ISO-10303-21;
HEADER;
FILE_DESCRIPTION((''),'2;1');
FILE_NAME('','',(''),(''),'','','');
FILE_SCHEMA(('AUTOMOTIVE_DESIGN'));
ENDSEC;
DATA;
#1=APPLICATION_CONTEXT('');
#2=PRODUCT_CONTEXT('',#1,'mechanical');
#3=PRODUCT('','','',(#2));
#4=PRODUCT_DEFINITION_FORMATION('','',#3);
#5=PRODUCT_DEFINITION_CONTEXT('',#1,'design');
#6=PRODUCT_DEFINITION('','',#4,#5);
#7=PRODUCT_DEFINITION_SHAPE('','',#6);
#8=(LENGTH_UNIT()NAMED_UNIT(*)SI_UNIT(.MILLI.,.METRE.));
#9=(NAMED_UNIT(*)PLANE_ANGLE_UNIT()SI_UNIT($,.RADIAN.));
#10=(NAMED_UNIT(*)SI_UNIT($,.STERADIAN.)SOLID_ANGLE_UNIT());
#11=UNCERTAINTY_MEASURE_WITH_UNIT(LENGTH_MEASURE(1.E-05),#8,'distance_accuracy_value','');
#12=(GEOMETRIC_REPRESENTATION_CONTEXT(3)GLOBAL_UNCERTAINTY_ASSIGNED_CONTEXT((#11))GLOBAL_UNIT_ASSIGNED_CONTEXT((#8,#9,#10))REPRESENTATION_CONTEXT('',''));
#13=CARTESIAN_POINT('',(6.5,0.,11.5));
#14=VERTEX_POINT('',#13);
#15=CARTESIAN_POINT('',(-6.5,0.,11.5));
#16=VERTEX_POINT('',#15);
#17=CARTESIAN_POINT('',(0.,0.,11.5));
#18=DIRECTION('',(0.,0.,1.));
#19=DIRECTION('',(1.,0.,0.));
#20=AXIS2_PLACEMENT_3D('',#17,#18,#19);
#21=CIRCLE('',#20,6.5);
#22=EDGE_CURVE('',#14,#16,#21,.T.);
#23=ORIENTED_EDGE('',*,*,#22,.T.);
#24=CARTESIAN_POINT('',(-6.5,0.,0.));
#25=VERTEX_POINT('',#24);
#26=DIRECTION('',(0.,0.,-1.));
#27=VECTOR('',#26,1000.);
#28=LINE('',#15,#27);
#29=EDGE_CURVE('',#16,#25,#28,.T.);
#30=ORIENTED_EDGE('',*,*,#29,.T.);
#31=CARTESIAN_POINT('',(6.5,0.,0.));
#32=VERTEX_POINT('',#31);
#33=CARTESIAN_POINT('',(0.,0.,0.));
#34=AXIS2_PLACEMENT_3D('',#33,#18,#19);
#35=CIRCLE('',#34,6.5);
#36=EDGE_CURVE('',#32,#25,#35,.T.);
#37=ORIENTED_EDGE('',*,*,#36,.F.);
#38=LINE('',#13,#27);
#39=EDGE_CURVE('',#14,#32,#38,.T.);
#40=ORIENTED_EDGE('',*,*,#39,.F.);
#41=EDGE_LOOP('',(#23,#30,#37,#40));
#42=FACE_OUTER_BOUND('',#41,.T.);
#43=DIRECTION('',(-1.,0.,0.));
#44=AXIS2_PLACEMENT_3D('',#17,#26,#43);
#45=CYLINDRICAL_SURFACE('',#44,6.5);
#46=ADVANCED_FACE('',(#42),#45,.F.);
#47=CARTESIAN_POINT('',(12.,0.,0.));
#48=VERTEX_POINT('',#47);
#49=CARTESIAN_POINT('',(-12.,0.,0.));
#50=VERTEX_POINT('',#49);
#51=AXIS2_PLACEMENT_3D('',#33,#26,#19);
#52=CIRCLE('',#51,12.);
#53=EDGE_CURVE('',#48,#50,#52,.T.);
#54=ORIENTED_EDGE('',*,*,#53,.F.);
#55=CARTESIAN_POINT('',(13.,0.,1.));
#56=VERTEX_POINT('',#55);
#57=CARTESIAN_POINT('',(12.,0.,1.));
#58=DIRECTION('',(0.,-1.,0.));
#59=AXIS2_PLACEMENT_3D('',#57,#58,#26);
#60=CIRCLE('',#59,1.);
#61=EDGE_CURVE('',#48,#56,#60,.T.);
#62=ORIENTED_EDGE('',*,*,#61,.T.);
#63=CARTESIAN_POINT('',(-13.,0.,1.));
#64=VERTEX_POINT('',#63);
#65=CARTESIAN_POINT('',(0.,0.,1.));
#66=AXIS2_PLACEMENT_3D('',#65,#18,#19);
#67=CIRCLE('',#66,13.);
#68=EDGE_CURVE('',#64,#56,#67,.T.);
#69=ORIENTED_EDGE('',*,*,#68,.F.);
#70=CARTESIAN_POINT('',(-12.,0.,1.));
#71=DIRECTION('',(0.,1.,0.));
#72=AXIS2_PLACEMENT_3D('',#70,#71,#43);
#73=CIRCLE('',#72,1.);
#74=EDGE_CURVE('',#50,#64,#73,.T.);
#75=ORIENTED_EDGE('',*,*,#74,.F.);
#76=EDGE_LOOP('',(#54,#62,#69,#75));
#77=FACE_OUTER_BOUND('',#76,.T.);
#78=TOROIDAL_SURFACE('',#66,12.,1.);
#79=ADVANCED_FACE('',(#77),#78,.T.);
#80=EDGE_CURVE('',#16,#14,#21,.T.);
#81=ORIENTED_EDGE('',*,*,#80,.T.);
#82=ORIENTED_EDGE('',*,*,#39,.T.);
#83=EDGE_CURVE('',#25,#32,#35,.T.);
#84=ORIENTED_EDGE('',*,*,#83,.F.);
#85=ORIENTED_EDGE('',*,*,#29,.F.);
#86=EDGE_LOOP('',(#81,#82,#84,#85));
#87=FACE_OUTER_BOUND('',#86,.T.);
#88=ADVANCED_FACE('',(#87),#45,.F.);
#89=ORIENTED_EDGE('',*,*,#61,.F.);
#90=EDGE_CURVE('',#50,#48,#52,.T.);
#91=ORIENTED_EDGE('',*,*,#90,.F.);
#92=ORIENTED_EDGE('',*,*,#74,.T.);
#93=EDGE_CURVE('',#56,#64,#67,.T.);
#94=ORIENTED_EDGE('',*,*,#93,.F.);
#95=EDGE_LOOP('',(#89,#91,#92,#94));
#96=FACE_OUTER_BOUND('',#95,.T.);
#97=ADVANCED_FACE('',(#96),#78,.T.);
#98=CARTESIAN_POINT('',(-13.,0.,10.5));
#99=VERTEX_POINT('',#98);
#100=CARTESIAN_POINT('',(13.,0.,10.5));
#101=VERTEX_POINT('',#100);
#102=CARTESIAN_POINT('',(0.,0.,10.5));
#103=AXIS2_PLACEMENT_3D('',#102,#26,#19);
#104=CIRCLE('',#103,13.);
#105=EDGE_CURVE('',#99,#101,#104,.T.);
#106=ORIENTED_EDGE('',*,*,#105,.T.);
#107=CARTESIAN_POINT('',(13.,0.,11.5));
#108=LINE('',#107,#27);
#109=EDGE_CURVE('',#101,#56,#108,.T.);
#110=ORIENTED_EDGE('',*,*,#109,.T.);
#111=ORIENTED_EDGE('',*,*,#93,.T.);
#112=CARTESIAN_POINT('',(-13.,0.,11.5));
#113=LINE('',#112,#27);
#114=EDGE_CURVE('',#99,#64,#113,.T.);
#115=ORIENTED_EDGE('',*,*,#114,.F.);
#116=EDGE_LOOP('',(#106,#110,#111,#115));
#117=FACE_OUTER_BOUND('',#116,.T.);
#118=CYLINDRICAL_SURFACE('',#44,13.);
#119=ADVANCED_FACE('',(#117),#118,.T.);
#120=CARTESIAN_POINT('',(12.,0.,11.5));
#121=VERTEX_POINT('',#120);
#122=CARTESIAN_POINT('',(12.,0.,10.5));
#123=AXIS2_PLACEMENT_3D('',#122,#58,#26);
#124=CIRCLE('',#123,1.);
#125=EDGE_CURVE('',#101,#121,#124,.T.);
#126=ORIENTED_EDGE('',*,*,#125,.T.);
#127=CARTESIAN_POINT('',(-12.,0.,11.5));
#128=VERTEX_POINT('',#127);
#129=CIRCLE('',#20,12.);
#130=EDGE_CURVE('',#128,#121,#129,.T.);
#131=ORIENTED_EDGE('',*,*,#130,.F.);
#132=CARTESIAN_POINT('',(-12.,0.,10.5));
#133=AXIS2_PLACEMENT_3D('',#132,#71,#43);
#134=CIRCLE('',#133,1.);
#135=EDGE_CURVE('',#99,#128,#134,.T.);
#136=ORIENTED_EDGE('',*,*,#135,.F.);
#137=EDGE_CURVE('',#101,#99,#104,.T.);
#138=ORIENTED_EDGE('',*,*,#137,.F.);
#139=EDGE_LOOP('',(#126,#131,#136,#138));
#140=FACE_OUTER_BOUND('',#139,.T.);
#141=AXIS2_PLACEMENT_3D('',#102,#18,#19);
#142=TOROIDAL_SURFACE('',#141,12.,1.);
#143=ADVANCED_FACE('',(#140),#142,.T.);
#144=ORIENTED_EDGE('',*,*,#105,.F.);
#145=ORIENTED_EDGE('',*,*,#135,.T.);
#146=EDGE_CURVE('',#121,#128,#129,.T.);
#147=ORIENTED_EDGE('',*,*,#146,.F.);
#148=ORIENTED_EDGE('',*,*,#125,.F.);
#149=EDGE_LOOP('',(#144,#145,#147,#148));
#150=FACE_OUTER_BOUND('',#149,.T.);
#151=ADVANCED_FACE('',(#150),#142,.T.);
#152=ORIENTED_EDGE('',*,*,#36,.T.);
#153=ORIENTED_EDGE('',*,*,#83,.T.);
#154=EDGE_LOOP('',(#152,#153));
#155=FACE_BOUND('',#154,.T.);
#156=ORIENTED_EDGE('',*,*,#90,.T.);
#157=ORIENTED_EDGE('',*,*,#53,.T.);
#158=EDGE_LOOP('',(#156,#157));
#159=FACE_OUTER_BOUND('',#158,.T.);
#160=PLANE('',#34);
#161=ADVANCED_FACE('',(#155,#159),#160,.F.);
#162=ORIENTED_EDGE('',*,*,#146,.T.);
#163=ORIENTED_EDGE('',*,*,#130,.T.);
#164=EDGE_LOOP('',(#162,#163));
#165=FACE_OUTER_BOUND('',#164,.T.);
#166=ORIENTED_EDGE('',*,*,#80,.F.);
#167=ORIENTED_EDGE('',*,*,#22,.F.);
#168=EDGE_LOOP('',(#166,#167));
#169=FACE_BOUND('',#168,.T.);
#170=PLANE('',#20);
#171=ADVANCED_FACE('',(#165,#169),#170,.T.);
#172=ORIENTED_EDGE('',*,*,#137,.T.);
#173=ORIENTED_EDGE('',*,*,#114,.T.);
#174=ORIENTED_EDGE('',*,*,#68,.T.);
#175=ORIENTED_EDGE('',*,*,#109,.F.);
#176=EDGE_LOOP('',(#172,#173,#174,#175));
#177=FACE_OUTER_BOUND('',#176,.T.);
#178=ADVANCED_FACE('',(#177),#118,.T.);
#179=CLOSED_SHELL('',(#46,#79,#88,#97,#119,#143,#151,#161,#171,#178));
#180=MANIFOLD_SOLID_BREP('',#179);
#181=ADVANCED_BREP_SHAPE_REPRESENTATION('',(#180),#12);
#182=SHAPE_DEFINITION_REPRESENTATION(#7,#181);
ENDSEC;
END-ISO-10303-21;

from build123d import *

# Parameters (mm, degrees)
SKETCH_1_R      = 13
SKETCH_1_R_2    = 6.5
EXTRUDE_1_DEPTH = 11.5
FILLET_1_R      = 1


with BuildPart() as part:
    # 草图1 → 凸台-拉伸1 (new body)
    with BuildSketch(Plane.XY):
        Circle(SKETCH_1_R)
        Circle(SKETCH_1_R_2, mode=Mode.SUBTRACT)
    extrude(amount=EXTRUDE_1_DEPTH)

    # 圆角1
    fillet_1_edges = [part.edges().sort_by_distance(p)[0] for p in [
        (-13, 0, 0),
        (-13, 0, 11.5),
    ]]
    fillet(fillet_1_edges, radius=FILLET_1_R)


solid = part.part
